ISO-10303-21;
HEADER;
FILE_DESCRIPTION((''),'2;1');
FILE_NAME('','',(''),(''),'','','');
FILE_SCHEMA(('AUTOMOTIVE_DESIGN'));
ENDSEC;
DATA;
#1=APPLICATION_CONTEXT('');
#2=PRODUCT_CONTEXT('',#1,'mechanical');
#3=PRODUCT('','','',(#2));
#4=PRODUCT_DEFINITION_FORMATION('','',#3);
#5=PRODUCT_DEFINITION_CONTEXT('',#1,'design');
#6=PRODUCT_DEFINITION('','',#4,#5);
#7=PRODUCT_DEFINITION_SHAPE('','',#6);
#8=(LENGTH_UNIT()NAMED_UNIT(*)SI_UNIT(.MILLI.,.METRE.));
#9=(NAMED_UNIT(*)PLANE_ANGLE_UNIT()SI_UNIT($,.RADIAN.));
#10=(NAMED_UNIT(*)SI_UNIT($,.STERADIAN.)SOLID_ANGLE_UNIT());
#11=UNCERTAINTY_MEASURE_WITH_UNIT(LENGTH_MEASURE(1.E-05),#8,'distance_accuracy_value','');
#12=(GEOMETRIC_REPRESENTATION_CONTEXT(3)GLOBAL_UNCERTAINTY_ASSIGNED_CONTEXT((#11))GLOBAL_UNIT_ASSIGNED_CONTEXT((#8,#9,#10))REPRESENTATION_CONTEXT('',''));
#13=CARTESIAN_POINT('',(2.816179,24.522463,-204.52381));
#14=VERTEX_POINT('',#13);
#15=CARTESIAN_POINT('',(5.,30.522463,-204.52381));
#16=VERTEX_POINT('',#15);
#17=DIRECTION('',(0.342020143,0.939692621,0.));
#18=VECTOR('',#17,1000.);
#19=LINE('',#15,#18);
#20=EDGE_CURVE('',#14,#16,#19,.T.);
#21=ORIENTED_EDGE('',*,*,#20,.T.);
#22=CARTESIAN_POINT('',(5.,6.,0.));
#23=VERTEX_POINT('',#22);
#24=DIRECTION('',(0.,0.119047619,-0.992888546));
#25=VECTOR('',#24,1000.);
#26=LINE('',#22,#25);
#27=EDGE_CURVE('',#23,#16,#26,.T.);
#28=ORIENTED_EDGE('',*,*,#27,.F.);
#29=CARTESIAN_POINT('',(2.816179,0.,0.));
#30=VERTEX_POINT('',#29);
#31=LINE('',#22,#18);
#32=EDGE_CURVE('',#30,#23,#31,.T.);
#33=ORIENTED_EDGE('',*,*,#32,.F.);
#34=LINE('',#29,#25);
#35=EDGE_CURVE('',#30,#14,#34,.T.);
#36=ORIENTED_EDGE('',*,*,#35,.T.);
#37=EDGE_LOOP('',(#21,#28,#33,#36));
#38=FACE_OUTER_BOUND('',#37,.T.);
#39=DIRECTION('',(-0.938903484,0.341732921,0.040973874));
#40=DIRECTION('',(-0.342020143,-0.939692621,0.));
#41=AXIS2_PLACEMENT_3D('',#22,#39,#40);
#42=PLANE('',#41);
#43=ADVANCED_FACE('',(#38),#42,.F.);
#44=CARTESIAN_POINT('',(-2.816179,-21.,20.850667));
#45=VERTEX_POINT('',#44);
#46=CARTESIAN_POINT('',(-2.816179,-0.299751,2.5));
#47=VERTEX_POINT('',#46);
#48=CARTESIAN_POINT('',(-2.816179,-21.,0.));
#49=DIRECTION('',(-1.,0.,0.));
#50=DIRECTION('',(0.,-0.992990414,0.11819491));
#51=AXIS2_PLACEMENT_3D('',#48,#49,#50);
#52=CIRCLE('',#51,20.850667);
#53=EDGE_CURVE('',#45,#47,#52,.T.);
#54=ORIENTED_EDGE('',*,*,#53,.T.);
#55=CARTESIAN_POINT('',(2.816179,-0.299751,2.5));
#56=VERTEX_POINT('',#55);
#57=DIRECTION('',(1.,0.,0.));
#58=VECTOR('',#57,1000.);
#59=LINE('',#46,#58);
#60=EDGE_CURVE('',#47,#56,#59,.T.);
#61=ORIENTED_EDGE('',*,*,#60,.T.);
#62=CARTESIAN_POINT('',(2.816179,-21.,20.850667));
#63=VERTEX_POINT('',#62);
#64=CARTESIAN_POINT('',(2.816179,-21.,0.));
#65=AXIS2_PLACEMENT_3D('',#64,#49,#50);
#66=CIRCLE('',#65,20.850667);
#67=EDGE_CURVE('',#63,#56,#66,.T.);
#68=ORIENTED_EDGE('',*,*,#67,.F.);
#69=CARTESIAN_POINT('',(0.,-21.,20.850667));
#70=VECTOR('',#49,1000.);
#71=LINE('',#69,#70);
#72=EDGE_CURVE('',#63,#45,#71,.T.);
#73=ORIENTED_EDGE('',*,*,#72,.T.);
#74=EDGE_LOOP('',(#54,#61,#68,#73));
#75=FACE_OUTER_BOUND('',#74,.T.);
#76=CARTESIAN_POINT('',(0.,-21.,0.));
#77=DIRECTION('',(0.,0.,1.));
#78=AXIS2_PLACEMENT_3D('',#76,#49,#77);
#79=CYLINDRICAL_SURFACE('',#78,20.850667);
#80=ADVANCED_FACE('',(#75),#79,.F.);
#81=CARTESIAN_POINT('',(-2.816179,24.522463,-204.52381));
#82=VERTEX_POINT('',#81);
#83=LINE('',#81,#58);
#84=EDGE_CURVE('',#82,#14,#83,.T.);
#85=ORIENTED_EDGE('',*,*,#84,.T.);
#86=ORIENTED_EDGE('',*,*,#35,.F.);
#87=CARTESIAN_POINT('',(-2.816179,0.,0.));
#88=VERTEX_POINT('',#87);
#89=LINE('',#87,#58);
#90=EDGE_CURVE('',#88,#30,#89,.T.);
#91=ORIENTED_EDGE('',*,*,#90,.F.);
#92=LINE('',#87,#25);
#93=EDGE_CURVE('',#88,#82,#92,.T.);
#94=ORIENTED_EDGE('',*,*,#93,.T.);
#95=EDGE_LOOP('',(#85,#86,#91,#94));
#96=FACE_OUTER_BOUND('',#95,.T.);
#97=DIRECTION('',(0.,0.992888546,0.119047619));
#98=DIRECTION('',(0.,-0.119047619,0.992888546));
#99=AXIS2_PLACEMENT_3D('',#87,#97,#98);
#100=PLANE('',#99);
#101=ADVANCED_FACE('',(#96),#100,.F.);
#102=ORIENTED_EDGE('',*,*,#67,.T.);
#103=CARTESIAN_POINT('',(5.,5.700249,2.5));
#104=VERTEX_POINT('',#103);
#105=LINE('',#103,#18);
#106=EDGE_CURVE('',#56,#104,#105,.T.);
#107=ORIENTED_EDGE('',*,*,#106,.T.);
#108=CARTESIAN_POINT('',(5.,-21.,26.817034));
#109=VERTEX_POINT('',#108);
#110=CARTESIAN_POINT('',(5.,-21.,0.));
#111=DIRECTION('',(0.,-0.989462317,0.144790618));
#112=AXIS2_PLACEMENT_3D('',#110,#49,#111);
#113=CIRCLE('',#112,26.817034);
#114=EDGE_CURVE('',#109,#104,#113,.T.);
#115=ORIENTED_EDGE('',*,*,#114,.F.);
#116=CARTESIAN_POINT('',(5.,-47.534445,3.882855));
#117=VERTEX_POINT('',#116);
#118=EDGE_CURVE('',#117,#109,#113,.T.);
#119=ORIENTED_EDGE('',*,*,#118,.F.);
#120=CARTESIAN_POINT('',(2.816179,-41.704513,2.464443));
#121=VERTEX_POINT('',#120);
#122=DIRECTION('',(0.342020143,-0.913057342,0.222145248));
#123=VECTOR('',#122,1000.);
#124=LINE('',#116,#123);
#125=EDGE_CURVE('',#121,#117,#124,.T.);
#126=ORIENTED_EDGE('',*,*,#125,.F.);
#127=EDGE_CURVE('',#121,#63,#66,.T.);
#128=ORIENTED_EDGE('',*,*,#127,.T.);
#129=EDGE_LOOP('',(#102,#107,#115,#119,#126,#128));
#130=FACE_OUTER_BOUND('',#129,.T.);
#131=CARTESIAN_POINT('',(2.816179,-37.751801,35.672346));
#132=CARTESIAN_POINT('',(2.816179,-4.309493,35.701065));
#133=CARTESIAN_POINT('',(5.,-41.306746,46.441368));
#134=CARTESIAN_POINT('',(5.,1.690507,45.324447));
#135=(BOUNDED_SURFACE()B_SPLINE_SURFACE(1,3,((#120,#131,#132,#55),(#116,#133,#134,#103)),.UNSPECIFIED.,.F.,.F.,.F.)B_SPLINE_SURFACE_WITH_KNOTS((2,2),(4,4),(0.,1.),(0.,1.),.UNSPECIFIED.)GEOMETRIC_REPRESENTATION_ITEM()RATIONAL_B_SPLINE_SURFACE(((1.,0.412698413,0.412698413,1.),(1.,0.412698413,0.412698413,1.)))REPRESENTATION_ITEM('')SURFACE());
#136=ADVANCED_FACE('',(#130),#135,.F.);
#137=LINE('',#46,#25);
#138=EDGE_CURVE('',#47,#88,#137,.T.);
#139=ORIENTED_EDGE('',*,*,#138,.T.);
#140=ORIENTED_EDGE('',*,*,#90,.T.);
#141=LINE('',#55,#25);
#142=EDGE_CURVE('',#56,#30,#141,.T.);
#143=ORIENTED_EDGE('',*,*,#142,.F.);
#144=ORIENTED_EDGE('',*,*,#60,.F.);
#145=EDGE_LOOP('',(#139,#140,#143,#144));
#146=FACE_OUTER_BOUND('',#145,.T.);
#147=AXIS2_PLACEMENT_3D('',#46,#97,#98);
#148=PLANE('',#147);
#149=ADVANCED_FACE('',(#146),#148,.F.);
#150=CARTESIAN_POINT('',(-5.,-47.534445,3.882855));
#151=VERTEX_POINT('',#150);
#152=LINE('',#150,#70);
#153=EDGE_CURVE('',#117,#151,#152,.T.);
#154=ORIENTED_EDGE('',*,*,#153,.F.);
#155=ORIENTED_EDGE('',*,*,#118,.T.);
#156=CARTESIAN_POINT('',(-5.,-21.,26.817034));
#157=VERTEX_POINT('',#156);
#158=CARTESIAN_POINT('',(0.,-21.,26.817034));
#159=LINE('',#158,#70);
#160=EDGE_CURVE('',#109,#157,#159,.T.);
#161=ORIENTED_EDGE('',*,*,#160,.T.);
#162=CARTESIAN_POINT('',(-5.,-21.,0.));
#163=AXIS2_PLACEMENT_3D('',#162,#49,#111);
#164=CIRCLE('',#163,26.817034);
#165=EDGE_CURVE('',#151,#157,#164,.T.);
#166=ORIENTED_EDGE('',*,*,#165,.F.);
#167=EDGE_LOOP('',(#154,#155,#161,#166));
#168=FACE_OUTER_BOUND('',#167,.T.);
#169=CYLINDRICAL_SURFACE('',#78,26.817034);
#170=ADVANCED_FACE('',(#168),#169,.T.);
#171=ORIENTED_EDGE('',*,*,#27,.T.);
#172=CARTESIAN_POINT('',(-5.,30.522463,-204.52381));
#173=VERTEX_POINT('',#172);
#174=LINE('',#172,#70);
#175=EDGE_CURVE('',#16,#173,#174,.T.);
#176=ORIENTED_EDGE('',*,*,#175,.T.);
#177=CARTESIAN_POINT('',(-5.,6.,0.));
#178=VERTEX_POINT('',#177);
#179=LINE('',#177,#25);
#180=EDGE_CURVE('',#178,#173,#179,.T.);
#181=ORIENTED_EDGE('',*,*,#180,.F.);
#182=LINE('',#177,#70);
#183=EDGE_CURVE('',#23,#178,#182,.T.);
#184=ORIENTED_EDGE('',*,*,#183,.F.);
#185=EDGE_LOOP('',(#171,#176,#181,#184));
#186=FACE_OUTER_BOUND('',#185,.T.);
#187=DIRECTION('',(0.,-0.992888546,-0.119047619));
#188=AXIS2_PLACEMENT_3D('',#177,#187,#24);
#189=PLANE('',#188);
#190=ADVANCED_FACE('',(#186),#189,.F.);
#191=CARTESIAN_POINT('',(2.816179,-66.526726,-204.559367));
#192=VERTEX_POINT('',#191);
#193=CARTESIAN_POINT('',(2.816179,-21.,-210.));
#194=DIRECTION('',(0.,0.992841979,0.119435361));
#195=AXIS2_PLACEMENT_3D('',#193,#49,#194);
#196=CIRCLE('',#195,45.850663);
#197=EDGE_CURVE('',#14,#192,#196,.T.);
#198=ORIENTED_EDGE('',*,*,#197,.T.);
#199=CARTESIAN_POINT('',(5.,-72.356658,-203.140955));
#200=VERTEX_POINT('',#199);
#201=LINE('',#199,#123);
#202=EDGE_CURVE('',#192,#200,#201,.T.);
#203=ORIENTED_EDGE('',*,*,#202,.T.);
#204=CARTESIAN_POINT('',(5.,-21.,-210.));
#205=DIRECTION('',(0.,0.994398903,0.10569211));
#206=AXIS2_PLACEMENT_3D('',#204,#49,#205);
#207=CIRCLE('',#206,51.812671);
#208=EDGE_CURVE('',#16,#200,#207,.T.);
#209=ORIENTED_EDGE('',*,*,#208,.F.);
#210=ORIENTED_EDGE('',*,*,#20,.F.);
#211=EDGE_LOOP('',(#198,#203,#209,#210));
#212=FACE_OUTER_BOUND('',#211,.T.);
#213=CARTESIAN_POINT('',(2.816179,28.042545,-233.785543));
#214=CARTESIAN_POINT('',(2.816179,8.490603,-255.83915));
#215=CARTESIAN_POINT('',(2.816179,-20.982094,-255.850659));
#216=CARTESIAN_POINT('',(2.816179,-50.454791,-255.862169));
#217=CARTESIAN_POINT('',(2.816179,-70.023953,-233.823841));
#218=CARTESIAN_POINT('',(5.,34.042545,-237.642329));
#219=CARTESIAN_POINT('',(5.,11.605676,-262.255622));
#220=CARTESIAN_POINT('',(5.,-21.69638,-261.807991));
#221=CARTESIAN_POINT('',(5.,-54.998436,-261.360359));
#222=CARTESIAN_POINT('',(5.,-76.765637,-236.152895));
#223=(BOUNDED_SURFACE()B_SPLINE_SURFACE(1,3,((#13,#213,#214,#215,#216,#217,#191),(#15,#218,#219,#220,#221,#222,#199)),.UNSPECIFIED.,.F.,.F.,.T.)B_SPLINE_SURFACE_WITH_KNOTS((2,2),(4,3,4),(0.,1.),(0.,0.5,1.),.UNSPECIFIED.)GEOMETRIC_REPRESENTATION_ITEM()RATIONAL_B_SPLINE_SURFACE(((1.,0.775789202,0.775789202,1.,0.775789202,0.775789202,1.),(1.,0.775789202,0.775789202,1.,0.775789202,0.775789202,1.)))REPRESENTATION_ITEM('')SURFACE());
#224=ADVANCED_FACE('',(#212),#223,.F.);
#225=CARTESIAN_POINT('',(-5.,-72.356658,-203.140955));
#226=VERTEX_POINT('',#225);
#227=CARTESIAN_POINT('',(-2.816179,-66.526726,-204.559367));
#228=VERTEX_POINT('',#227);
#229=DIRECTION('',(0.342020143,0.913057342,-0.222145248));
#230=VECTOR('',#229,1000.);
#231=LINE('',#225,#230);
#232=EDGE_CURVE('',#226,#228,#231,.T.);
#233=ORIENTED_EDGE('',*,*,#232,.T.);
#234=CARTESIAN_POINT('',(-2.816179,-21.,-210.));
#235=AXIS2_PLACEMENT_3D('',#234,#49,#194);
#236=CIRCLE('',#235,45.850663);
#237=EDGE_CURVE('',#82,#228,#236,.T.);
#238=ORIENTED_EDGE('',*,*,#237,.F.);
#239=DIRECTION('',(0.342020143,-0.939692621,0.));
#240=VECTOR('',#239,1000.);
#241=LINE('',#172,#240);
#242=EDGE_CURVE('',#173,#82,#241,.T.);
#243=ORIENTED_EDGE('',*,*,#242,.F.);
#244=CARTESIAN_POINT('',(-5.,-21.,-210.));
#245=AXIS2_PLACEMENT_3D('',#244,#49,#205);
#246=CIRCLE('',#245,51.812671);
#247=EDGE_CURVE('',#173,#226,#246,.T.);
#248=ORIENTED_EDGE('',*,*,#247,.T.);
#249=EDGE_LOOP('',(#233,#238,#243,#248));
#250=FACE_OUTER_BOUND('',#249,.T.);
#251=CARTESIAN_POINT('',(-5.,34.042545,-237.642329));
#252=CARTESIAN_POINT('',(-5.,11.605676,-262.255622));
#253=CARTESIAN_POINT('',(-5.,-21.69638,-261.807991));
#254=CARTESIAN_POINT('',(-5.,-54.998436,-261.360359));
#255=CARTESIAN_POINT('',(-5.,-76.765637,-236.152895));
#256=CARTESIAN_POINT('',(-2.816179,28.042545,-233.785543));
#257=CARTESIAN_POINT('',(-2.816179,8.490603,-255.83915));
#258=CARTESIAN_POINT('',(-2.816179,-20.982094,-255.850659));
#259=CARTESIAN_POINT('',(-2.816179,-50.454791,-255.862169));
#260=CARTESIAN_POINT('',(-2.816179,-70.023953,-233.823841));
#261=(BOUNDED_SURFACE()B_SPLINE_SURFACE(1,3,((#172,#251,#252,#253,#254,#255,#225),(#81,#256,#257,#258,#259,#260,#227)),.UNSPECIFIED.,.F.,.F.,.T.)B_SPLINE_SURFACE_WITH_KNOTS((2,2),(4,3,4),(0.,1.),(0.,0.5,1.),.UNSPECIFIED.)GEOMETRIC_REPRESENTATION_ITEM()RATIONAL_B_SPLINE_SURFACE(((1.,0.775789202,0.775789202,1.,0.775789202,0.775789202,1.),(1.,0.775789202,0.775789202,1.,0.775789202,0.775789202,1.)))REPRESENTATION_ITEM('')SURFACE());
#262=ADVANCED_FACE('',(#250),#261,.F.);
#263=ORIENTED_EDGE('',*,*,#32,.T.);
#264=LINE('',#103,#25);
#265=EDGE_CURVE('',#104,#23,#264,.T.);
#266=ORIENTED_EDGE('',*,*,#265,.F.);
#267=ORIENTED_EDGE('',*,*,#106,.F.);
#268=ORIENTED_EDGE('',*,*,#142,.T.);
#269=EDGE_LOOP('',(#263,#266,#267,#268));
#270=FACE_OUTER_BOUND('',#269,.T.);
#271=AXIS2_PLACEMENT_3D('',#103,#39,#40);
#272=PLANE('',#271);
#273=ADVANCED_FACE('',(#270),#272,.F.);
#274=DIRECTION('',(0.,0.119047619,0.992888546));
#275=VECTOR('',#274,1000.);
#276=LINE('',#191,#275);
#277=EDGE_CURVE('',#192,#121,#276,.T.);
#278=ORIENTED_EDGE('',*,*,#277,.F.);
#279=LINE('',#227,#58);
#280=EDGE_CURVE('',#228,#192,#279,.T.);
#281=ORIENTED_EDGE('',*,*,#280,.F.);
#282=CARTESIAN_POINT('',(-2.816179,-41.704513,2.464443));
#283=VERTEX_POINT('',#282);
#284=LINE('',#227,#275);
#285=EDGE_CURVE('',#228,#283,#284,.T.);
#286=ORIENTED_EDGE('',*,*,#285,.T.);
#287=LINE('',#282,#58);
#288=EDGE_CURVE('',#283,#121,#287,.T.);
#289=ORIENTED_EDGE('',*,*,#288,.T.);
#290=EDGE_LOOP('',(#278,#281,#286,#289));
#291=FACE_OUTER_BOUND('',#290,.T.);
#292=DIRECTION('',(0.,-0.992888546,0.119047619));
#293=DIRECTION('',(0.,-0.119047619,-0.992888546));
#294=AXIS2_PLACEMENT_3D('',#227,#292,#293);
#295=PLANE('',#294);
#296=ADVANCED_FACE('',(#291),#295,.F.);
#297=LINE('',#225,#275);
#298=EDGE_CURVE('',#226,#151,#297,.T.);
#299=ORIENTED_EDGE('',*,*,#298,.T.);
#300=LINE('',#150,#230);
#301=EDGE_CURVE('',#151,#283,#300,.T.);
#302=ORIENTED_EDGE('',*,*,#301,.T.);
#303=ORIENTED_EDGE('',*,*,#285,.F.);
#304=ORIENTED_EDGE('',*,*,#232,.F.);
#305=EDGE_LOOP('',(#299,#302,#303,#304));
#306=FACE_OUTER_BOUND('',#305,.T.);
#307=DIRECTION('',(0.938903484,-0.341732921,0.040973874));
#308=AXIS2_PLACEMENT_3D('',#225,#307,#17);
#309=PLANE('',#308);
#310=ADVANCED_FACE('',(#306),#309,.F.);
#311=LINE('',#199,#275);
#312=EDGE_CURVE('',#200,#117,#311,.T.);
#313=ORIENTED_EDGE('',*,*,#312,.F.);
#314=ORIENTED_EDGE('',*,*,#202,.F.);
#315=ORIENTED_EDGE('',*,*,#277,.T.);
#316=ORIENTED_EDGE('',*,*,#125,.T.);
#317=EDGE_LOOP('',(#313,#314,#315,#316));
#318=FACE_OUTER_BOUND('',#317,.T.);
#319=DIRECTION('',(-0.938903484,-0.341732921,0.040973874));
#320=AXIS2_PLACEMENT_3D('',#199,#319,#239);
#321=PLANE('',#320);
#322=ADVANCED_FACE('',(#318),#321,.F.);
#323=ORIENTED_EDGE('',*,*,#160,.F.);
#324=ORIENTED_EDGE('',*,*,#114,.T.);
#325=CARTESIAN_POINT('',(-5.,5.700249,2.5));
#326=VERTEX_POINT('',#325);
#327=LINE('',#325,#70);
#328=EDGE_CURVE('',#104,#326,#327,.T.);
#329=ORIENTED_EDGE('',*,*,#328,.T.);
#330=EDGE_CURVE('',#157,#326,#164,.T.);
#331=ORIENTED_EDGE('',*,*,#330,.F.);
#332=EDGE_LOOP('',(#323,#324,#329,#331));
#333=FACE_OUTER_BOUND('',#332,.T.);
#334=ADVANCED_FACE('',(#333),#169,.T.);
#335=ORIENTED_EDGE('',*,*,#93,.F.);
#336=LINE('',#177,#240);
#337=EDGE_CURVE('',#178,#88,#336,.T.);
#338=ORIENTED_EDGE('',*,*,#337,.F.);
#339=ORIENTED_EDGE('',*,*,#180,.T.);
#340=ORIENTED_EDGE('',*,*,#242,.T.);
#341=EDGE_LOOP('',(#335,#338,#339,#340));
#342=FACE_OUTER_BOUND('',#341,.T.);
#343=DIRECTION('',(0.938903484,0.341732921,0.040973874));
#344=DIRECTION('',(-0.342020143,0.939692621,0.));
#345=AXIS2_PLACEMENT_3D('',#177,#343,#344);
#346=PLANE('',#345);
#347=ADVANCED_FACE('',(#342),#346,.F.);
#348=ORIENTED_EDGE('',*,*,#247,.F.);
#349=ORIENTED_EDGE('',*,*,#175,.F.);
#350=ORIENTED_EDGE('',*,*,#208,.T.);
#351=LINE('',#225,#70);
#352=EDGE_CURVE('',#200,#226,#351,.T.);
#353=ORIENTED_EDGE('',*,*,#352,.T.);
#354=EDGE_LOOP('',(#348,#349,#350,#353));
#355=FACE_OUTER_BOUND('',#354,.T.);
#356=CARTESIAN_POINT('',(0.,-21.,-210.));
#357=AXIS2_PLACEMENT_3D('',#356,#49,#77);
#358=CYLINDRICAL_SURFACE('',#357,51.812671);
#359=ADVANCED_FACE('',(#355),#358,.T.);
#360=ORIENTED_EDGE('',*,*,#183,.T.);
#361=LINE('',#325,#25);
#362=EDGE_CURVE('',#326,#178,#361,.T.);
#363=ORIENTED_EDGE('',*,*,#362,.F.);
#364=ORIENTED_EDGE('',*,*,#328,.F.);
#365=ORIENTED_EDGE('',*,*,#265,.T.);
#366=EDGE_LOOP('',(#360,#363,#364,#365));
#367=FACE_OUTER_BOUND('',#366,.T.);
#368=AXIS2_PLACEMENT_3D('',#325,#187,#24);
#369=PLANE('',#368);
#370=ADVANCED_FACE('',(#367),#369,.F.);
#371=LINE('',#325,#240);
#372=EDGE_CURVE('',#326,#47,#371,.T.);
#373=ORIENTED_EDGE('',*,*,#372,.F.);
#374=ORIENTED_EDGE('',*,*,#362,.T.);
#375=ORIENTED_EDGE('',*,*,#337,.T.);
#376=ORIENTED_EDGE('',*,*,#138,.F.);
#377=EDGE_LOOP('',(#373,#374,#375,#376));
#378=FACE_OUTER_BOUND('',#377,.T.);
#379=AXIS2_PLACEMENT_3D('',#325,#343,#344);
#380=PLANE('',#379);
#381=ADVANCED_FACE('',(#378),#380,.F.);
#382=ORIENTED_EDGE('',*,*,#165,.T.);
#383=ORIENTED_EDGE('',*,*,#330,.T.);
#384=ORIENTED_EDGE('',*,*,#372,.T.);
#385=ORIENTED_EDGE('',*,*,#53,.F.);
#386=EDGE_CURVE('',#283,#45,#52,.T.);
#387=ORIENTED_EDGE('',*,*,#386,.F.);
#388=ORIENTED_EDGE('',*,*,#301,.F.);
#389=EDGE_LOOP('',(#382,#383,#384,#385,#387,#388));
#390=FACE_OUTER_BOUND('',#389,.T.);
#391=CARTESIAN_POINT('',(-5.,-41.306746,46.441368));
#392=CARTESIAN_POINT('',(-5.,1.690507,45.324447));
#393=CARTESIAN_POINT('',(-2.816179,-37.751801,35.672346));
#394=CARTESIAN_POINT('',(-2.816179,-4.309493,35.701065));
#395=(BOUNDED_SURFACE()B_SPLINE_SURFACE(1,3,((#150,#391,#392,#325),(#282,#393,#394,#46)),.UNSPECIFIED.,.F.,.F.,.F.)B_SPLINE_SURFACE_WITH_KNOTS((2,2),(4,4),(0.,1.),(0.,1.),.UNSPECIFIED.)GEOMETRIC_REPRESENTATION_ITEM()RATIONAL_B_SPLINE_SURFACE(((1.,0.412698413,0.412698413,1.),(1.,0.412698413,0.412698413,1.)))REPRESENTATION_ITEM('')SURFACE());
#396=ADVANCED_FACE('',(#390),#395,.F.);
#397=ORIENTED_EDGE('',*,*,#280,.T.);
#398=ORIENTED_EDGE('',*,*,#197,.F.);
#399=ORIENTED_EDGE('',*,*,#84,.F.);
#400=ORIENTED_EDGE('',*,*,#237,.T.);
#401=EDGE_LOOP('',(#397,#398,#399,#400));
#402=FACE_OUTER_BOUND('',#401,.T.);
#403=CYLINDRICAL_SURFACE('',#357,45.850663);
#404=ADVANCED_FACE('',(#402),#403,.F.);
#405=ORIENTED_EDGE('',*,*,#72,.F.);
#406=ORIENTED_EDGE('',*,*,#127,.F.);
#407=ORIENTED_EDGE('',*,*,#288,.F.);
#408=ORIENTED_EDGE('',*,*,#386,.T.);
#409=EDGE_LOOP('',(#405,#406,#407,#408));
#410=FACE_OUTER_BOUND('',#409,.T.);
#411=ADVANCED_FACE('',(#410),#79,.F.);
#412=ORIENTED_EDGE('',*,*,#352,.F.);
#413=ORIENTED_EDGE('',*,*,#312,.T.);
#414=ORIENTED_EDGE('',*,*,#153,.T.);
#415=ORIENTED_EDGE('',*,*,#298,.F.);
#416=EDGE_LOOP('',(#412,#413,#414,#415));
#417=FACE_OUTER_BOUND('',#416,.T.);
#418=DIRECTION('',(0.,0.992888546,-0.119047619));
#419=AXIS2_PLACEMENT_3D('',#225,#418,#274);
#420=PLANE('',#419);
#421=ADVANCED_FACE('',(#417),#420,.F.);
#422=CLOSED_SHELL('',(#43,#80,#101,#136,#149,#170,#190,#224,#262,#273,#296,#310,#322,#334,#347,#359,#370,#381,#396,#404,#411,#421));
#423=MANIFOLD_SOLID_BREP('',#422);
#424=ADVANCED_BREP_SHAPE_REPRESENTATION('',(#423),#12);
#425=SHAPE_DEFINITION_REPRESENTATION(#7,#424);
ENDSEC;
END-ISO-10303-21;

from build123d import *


with BuildPart() as part:
    # Sweep1: sweep along a path in Sketch3
    with BuildLine(Plane(origin=(0, 0, 0), x_dir=(0, 0, -1), z_dir=(1, 0, 0))) as sweep1_path:
        Line((-2.5, -0.149340538), (204.523809524, 24.672873107))
        ThreePointArc((204.523809524, 24.672873107), (256, -21), (204.523809524, -66.672873107))
        Line((204.523809524, -66.672873107), (-2.5, -41.850659462))
        ThreePointArc((-2.5, -41.850659462), (-21, -21), (-2.5, -0.149340538))
    # Sketch2 → Sweep1 (sweep)
    with BuildSketch(Plane.XY):
        Polygon((-5, 6), (5, 6), (2.816178594, 0), (-2.816178594, 0), align=None)
    sweep(path=sweep1_path.line)


solid = part.part
